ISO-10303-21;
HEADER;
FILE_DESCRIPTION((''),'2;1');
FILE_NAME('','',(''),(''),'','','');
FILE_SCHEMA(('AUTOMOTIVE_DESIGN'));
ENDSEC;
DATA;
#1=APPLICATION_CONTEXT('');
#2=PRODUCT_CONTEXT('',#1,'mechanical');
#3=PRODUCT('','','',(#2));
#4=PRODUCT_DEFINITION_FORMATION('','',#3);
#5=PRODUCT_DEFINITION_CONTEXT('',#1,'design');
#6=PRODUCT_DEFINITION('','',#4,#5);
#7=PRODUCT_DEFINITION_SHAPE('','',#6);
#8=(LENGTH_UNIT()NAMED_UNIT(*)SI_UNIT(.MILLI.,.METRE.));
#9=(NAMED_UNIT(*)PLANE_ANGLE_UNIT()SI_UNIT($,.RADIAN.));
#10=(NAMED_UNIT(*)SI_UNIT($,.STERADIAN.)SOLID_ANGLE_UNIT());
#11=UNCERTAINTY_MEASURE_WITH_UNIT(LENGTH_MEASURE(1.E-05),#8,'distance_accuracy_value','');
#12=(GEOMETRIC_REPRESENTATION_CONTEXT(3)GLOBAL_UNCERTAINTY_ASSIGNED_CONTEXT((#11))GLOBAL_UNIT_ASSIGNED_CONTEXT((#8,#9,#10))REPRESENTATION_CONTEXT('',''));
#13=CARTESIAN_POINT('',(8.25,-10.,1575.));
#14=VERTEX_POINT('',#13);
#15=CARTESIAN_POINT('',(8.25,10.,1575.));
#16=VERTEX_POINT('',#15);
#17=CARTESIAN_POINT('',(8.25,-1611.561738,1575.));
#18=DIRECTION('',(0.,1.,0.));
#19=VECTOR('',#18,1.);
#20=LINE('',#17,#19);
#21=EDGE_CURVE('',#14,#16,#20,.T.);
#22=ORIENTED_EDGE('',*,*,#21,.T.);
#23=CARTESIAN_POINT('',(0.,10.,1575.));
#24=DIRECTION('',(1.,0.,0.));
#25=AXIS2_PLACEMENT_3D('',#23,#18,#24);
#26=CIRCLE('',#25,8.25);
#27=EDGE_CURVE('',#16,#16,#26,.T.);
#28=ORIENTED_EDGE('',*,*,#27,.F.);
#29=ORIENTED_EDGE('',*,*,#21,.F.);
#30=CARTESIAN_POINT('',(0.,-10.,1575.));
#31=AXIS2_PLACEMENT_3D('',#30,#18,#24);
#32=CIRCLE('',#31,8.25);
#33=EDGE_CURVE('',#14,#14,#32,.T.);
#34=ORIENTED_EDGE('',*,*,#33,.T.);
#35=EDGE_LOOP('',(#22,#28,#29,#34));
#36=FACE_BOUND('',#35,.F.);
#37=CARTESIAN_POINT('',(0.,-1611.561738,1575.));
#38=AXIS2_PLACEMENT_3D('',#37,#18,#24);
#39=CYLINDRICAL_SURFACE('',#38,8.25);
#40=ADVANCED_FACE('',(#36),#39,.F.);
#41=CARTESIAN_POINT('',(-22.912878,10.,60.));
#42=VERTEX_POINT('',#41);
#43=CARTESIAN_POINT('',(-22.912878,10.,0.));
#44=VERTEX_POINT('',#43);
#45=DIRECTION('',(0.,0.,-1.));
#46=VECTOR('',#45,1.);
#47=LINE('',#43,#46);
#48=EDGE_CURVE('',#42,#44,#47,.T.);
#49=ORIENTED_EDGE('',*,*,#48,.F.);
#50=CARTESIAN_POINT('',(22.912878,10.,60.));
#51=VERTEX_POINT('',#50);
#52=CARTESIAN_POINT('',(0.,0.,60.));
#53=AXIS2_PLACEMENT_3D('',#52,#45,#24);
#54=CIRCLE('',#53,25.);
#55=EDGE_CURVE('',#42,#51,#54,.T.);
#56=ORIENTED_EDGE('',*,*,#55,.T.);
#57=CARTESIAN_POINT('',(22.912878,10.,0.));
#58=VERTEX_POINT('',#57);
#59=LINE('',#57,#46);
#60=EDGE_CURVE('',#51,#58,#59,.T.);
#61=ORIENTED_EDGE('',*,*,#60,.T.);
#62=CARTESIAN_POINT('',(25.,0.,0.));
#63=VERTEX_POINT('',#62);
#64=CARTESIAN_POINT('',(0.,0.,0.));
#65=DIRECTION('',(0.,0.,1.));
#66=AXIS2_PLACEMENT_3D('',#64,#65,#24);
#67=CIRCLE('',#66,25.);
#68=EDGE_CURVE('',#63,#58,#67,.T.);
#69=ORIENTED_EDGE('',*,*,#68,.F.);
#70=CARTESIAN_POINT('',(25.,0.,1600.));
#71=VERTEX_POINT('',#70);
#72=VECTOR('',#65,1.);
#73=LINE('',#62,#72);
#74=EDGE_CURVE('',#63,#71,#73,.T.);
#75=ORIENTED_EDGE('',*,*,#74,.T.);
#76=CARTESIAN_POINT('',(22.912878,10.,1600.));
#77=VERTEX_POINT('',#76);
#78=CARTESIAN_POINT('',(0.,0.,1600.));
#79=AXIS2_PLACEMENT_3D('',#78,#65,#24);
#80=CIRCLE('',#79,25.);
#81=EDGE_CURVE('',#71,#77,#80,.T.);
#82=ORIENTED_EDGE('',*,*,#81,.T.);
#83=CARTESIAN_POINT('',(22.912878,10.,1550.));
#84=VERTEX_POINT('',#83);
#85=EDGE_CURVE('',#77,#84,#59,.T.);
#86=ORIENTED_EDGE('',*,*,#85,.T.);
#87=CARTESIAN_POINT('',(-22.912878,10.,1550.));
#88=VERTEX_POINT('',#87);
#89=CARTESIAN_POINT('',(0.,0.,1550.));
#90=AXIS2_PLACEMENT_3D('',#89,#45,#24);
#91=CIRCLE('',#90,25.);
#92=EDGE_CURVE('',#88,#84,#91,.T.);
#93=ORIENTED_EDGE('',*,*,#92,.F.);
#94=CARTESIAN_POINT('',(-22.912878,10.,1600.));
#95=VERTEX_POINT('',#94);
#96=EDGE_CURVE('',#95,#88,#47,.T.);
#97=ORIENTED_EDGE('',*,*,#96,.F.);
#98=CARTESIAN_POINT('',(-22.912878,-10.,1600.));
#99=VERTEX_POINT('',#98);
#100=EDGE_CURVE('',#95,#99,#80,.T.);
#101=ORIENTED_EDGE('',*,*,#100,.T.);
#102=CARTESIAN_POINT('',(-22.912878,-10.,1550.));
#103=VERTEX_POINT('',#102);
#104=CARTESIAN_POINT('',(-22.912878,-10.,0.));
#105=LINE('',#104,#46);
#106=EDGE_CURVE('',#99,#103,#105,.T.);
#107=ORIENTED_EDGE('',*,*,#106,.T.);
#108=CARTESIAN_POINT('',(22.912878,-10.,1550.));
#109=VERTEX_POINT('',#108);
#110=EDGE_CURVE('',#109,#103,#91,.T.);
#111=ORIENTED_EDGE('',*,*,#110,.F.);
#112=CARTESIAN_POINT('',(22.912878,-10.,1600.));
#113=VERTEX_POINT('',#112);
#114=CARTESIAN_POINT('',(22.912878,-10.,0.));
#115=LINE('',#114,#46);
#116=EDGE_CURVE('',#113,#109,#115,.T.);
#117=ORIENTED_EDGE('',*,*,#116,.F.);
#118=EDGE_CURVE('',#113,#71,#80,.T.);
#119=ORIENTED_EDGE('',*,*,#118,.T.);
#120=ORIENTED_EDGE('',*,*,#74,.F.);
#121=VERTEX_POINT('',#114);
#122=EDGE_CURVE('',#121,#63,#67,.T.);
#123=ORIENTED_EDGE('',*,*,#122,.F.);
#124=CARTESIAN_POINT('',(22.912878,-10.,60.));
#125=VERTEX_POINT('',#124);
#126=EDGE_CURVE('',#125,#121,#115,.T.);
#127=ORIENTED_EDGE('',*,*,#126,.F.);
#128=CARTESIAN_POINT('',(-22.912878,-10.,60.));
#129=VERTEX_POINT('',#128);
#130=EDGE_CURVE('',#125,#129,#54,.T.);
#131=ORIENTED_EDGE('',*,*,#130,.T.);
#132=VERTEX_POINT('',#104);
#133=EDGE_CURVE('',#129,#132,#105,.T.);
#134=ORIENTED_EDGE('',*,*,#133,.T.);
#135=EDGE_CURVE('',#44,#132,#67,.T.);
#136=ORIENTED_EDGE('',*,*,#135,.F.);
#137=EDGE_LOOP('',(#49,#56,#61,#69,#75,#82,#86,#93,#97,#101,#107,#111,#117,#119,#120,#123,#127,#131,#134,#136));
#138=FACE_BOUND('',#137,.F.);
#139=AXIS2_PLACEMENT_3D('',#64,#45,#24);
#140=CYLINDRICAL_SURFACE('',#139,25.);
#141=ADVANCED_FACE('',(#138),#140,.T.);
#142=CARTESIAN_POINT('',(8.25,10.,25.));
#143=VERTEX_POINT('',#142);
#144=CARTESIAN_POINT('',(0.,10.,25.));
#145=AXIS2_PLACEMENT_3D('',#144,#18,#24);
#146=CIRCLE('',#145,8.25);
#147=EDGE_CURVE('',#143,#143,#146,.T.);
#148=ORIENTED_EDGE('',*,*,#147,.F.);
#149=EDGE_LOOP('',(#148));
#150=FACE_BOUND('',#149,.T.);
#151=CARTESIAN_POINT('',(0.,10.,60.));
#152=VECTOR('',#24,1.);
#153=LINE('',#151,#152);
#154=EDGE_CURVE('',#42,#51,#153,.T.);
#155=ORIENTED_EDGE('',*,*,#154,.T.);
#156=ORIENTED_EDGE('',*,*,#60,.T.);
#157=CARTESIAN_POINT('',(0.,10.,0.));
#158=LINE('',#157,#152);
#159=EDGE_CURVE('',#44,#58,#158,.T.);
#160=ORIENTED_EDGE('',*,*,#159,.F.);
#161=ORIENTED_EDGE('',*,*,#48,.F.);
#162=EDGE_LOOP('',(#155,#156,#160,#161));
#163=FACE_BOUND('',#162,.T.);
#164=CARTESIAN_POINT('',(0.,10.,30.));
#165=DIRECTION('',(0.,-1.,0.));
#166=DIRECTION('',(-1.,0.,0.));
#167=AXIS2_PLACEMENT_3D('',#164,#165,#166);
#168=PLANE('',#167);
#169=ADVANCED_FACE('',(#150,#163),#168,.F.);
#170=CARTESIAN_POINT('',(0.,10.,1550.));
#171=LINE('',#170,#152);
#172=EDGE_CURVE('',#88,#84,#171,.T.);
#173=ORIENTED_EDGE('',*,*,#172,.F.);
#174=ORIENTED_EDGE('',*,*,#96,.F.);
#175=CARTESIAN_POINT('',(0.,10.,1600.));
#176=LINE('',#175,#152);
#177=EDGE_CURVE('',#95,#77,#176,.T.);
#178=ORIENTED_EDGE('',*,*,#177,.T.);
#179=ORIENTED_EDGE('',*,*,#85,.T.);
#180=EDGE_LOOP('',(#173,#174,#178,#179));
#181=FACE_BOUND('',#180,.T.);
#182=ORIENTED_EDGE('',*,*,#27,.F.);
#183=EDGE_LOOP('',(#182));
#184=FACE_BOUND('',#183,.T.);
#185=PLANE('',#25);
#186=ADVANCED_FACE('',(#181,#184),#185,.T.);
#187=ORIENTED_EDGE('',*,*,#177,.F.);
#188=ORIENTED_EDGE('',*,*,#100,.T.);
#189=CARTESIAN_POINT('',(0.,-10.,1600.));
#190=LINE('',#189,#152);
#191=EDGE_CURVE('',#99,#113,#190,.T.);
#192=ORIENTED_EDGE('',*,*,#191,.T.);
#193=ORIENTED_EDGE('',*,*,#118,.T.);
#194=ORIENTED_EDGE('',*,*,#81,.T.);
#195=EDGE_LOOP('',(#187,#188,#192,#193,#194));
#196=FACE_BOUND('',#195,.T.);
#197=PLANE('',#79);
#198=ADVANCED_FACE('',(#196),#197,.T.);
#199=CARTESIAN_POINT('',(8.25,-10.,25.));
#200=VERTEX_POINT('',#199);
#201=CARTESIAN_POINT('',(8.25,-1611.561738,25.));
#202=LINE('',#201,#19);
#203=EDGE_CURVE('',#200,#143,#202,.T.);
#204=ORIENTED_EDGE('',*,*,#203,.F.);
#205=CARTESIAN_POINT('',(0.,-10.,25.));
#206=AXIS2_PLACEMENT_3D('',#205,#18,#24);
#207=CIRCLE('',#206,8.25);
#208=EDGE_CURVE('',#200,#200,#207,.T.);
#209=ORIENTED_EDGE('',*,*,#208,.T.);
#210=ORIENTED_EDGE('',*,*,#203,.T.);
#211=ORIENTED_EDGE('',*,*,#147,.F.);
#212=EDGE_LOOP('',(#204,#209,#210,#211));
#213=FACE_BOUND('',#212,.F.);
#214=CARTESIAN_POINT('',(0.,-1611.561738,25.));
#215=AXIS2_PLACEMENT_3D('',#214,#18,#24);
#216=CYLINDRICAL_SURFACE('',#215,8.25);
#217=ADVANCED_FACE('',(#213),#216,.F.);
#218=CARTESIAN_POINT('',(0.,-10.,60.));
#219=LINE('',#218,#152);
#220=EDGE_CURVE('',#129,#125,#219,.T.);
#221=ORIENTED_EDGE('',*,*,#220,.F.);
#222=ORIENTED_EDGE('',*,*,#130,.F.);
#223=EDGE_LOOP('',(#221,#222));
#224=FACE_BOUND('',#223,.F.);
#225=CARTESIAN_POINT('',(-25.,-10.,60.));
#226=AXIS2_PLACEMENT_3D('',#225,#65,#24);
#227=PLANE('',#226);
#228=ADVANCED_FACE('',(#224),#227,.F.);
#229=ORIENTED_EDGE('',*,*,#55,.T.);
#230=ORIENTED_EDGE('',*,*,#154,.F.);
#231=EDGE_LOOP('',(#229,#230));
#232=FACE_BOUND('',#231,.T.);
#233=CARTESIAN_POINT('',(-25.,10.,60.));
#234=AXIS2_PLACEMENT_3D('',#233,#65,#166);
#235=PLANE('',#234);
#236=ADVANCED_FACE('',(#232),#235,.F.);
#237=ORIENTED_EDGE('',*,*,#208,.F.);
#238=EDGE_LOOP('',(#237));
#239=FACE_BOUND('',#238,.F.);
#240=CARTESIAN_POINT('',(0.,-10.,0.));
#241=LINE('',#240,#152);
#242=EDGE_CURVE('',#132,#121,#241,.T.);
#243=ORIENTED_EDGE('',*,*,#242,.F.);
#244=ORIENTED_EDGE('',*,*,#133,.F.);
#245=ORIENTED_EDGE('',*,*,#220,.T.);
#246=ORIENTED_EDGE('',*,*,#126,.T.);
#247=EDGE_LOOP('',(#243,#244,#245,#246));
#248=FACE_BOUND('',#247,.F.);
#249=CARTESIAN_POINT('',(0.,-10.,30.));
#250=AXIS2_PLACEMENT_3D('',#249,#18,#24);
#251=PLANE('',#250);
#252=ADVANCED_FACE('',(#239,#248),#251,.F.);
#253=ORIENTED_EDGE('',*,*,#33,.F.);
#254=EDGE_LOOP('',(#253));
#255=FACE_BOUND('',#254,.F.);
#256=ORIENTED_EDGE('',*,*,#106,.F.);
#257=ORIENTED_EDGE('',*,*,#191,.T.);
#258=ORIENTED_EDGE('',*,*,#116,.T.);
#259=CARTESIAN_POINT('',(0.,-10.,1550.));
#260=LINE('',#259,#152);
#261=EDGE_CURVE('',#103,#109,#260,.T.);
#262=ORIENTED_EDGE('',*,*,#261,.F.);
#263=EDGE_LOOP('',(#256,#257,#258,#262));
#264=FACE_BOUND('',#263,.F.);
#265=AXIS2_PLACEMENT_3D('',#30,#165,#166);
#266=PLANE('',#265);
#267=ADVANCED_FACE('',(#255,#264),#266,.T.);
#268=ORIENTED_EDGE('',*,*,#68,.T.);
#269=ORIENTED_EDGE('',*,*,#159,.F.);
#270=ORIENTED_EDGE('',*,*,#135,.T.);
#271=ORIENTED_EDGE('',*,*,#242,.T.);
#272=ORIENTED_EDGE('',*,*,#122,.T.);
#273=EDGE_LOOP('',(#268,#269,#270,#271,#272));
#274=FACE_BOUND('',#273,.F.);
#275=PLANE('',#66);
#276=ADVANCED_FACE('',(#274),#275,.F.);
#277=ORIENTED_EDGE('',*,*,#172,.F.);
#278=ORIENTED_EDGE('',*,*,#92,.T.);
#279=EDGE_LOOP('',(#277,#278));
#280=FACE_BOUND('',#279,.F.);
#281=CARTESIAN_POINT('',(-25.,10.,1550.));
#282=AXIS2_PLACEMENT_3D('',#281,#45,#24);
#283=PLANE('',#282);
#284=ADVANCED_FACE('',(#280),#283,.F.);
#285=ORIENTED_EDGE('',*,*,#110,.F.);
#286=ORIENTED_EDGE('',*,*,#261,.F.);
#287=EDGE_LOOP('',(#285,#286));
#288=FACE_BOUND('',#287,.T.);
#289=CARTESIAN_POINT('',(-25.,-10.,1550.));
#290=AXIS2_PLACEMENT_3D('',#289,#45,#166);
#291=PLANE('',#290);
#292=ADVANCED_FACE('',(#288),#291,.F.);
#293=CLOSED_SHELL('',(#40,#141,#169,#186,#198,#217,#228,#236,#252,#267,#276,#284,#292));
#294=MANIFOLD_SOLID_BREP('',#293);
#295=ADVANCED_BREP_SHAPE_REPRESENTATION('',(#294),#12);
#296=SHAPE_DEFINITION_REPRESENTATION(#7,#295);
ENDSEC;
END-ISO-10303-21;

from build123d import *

# Parameters (mm, degrees)
SKETCH1_R           = 25
BOSS_EXTRUDE1_DEPTH = 1600
CUT_EXTRUDE1_START  = -10
SKETCH2_W           = 50
SKETCH2_H           = 60
CUT_EXTRUDE1_DEPTH  = 1000
F_16_5_16_5_HOLE1_D = 16.5
CUT_EXTRUDE2_START  = 10
SKETCH5_W           = 50
SKETCH5_H           = 50
CUT_EXTRUDE2_DEPTH  = 1000
F_16_5_16_5_HOLE2_D = 16.5


with BuildPart() as part:
    # Sketch1 → Boss-Extrude1 (new body)
    with BuildSketch(Plane.XY):
        Circle(SKETCH1_R)
    extrude(amount=BOSS_EXTRUDE1_DEPTH)

    # Sketch2 → Cut-Extrude1 (cut)
    with BuildSketch(Plane(origin=(0, 0, 0), x_dir=(1, 0, 0), z_dir=(0, 1, 0)).offset(CUT_EXTRUDE1_START)):
        with Locations((0, -30)):
            Rectangle(SKETCH2_W, SKETCH2_H)
    cut_extrude1 = extrude(amount=-CUT_EXTRUDE1_DEPTH, mode=Mode.SUBTRACT)

    # Mirror1: Cut-Extrude1 across plane
    add(cut_extrude1.mirror(Plane.ZX), mode=Mode.SUBTRACT)

    # Ø16.5 (16.5) Hole1 (through all)
    with Locations(Plane(origin=(0, -10, 0), x_dir=(-1, 0, 0), z_dir=(0, -1, 0))):
        with Locations((0, -25)):
            Hole(F_16_5_16_5_HOLE1_D / 2)

    # Sketch5 → Cut-Extrude2 (cut)
    with BuildSketch(Plane(origin=(0, 0, 0), x_dir=(1, 0, 0), z_dir=(0, 1, 0)).offset(CUT_EXTRUDE2_START)):
        with Locations((0, -1575)):
            Rectangle(SKETCH5_W, SKETCH5_H)
    cut_extrude2 = extrude(amount=CUT_EXTRUDE2_DEPTH, mode=Mode.SUBTRACT)

    # Mirror2: Cut-Extrude2 across plane
    add(cut_extrude2.mirror(Plane.ZX), mode=Mode.SUBTRACT)

    # Ø16.5 (16.5) Hole2 (through all)
    with Locations(Plane(origin=(0, -10, 0), x_dir=(-1, 0, 0), z_dir=(0, -1, 0))):
        with Locations((0, -1575)):
            Hole(F_16_5_16_5_HOLE2_D / 2)


solid = part.part
